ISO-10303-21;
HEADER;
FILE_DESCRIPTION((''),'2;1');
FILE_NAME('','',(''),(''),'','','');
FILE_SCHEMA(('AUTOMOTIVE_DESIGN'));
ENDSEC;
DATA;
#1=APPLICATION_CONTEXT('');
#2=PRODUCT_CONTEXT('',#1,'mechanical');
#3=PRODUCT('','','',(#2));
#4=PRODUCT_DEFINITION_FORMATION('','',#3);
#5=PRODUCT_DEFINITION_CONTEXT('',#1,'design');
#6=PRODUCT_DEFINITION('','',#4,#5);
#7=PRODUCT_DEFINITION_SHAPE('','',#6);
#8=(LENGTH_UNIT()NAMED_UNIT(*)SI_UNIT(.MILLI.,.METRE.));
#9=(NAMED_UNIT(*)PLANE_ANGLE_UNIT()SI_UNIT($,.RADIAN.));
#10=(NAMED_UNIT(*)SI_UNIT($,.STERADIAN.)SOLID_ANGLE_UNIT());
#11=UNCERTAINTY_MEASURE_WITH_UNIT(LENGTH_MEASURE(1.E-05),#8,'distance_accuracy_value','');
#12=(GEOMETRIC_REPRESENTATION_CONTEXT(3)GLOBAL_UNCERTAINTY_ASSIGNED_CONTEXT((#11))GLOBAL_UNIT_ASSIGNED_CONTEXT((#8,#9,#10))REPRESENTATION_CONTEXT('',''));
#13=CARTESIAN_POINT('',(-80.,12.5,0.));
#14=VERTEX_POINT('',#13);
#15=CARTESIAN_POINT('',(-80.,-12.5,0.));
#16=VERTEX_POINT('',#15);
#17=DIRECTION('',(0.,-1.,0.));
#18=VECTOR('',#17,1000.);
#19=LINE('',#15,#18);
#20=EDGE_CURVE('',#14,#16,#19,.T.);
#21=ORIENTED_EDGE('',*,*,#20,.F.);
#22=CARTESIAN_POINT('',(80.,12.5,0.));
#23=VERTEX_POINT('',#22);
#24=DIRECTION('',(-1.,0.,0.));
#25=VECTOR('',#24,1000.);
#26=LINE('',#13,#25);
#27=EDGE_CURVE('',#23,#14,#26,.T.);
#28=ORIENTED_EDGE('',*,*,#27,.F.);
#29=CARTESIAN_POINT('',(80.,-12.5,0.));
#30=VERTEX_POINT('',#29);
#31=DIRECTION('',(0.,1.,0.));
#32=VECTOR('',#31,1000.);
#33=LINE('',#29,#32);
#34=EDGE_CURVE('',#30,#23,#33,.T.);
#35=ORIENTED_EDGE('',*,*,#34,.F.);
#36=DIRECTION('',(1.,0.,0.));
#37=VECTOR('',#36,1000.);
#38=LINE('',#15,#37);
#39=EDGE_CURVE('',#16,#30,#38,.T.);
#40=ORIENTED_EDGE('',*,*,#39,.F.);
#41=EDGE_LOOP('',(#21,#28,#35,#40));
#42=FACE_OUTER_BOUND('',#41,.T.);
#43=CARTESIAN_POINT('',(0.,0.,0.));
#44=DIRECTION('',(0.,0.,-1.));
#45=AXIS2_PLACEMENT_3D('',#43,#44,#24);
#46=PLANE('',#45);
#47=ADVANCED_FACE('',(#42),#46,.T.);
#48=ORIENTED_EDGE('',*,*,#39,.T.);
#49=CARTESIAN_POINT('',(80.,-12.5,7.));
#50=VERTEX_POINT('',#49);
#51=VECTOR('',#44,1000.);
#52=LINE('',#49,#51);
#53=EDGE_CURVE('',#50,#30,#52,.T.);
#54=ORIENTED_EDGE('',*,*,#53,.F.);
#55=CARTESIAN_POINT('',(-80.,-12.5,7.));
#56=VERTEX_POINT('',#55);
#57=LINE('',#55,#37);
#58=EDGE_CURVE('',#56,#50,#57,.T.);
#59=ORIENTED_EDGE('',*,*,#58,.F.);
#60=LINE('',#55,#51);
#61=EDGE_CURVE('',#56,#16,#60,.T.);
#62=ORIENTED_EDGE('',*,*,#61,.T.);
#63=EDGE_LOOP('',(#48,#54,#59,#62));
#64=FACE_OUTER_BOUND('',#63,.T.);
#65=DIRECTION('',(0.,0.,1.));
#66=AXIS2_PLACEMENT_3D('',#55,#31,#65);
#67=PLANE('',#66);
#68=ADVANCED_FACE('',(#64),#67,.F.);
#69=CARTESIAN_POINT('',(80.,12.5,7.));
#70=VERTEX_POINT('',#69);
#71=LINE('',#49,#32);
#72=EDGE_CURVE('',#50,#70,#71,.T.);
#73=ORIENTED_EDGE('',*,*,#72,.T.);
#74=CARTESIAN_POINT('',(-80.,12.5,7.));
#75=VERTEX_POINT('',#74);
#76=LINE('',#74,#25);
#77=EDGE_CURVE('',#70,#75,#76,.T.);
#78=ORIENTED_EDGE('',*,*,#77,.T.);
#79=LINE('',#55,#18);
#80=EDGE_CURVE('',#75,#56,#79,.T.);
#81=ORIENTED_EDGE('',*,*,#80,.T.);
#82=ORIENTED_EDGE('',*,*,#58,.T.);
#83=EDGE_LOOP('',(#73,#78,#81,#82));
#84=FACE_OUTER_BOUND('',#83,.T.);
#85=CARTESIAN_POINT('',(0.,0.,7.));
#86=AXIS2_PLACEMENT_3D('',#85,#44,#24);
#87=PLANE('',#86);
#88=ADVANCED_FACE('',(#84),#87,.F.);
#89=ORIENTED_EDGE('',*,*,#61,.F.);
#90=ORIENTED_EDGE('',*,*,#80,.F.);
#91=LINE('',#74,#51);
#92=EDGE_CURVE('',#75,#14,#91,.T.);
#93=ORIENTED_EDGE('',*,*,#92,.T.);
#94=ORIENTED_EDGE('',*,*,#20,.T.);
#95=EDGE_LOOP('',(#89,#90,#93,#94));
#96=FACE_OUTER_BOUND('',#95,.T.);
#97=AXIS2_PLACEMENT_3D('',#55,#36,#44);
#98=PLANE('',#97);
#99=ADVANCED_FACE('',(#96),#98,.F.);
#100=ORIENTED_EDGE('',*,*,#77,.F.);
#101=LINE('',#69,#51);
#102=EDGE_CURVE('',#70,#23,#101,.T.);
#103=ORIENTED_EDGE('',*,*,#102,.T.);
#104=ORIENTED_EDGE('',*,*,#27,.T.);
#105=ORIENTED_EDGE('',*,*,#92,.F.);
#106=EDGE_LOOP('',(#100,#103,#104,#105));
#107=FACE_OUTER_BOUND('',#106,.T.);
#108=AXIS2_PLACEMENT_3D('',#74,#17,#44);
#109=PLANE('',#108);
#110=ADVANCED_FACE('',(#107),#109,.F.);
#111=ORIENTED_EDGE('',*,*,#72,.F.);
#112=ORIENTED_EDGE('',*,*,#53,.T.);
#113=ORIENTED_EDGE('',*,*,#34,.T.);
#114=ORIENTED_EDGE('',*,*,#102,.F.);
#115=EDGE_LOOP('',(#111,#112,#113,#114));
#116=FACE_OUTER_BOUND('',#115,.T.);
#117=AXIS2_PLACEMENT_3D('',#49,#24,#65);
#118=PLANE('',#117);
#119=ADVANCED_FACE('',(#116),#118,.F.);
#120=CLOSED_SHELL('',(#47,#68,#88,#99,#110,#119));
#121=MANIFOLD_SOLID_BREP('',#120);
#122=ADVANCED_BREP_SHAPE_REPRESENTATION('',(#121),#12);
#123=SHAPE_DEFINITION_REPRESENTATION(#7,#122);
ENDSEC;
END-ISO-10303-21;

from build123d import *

# Parameters (mm, degrees)
SKETCH_1_W      = 160
SKETCH_1_H      = 25
EXTRUDE_1_DEPTH = 7


with BuildPart() as part:
    # 草图1 → 凸台-拉伸1 (new body)
    with BuildSketch(Plane.XY):
        Rectangle(SKETCH_1_W, SKETCH_1_H)
    extrude(amount=EXTRUDE_1_DEPTH)


solid = part.part
